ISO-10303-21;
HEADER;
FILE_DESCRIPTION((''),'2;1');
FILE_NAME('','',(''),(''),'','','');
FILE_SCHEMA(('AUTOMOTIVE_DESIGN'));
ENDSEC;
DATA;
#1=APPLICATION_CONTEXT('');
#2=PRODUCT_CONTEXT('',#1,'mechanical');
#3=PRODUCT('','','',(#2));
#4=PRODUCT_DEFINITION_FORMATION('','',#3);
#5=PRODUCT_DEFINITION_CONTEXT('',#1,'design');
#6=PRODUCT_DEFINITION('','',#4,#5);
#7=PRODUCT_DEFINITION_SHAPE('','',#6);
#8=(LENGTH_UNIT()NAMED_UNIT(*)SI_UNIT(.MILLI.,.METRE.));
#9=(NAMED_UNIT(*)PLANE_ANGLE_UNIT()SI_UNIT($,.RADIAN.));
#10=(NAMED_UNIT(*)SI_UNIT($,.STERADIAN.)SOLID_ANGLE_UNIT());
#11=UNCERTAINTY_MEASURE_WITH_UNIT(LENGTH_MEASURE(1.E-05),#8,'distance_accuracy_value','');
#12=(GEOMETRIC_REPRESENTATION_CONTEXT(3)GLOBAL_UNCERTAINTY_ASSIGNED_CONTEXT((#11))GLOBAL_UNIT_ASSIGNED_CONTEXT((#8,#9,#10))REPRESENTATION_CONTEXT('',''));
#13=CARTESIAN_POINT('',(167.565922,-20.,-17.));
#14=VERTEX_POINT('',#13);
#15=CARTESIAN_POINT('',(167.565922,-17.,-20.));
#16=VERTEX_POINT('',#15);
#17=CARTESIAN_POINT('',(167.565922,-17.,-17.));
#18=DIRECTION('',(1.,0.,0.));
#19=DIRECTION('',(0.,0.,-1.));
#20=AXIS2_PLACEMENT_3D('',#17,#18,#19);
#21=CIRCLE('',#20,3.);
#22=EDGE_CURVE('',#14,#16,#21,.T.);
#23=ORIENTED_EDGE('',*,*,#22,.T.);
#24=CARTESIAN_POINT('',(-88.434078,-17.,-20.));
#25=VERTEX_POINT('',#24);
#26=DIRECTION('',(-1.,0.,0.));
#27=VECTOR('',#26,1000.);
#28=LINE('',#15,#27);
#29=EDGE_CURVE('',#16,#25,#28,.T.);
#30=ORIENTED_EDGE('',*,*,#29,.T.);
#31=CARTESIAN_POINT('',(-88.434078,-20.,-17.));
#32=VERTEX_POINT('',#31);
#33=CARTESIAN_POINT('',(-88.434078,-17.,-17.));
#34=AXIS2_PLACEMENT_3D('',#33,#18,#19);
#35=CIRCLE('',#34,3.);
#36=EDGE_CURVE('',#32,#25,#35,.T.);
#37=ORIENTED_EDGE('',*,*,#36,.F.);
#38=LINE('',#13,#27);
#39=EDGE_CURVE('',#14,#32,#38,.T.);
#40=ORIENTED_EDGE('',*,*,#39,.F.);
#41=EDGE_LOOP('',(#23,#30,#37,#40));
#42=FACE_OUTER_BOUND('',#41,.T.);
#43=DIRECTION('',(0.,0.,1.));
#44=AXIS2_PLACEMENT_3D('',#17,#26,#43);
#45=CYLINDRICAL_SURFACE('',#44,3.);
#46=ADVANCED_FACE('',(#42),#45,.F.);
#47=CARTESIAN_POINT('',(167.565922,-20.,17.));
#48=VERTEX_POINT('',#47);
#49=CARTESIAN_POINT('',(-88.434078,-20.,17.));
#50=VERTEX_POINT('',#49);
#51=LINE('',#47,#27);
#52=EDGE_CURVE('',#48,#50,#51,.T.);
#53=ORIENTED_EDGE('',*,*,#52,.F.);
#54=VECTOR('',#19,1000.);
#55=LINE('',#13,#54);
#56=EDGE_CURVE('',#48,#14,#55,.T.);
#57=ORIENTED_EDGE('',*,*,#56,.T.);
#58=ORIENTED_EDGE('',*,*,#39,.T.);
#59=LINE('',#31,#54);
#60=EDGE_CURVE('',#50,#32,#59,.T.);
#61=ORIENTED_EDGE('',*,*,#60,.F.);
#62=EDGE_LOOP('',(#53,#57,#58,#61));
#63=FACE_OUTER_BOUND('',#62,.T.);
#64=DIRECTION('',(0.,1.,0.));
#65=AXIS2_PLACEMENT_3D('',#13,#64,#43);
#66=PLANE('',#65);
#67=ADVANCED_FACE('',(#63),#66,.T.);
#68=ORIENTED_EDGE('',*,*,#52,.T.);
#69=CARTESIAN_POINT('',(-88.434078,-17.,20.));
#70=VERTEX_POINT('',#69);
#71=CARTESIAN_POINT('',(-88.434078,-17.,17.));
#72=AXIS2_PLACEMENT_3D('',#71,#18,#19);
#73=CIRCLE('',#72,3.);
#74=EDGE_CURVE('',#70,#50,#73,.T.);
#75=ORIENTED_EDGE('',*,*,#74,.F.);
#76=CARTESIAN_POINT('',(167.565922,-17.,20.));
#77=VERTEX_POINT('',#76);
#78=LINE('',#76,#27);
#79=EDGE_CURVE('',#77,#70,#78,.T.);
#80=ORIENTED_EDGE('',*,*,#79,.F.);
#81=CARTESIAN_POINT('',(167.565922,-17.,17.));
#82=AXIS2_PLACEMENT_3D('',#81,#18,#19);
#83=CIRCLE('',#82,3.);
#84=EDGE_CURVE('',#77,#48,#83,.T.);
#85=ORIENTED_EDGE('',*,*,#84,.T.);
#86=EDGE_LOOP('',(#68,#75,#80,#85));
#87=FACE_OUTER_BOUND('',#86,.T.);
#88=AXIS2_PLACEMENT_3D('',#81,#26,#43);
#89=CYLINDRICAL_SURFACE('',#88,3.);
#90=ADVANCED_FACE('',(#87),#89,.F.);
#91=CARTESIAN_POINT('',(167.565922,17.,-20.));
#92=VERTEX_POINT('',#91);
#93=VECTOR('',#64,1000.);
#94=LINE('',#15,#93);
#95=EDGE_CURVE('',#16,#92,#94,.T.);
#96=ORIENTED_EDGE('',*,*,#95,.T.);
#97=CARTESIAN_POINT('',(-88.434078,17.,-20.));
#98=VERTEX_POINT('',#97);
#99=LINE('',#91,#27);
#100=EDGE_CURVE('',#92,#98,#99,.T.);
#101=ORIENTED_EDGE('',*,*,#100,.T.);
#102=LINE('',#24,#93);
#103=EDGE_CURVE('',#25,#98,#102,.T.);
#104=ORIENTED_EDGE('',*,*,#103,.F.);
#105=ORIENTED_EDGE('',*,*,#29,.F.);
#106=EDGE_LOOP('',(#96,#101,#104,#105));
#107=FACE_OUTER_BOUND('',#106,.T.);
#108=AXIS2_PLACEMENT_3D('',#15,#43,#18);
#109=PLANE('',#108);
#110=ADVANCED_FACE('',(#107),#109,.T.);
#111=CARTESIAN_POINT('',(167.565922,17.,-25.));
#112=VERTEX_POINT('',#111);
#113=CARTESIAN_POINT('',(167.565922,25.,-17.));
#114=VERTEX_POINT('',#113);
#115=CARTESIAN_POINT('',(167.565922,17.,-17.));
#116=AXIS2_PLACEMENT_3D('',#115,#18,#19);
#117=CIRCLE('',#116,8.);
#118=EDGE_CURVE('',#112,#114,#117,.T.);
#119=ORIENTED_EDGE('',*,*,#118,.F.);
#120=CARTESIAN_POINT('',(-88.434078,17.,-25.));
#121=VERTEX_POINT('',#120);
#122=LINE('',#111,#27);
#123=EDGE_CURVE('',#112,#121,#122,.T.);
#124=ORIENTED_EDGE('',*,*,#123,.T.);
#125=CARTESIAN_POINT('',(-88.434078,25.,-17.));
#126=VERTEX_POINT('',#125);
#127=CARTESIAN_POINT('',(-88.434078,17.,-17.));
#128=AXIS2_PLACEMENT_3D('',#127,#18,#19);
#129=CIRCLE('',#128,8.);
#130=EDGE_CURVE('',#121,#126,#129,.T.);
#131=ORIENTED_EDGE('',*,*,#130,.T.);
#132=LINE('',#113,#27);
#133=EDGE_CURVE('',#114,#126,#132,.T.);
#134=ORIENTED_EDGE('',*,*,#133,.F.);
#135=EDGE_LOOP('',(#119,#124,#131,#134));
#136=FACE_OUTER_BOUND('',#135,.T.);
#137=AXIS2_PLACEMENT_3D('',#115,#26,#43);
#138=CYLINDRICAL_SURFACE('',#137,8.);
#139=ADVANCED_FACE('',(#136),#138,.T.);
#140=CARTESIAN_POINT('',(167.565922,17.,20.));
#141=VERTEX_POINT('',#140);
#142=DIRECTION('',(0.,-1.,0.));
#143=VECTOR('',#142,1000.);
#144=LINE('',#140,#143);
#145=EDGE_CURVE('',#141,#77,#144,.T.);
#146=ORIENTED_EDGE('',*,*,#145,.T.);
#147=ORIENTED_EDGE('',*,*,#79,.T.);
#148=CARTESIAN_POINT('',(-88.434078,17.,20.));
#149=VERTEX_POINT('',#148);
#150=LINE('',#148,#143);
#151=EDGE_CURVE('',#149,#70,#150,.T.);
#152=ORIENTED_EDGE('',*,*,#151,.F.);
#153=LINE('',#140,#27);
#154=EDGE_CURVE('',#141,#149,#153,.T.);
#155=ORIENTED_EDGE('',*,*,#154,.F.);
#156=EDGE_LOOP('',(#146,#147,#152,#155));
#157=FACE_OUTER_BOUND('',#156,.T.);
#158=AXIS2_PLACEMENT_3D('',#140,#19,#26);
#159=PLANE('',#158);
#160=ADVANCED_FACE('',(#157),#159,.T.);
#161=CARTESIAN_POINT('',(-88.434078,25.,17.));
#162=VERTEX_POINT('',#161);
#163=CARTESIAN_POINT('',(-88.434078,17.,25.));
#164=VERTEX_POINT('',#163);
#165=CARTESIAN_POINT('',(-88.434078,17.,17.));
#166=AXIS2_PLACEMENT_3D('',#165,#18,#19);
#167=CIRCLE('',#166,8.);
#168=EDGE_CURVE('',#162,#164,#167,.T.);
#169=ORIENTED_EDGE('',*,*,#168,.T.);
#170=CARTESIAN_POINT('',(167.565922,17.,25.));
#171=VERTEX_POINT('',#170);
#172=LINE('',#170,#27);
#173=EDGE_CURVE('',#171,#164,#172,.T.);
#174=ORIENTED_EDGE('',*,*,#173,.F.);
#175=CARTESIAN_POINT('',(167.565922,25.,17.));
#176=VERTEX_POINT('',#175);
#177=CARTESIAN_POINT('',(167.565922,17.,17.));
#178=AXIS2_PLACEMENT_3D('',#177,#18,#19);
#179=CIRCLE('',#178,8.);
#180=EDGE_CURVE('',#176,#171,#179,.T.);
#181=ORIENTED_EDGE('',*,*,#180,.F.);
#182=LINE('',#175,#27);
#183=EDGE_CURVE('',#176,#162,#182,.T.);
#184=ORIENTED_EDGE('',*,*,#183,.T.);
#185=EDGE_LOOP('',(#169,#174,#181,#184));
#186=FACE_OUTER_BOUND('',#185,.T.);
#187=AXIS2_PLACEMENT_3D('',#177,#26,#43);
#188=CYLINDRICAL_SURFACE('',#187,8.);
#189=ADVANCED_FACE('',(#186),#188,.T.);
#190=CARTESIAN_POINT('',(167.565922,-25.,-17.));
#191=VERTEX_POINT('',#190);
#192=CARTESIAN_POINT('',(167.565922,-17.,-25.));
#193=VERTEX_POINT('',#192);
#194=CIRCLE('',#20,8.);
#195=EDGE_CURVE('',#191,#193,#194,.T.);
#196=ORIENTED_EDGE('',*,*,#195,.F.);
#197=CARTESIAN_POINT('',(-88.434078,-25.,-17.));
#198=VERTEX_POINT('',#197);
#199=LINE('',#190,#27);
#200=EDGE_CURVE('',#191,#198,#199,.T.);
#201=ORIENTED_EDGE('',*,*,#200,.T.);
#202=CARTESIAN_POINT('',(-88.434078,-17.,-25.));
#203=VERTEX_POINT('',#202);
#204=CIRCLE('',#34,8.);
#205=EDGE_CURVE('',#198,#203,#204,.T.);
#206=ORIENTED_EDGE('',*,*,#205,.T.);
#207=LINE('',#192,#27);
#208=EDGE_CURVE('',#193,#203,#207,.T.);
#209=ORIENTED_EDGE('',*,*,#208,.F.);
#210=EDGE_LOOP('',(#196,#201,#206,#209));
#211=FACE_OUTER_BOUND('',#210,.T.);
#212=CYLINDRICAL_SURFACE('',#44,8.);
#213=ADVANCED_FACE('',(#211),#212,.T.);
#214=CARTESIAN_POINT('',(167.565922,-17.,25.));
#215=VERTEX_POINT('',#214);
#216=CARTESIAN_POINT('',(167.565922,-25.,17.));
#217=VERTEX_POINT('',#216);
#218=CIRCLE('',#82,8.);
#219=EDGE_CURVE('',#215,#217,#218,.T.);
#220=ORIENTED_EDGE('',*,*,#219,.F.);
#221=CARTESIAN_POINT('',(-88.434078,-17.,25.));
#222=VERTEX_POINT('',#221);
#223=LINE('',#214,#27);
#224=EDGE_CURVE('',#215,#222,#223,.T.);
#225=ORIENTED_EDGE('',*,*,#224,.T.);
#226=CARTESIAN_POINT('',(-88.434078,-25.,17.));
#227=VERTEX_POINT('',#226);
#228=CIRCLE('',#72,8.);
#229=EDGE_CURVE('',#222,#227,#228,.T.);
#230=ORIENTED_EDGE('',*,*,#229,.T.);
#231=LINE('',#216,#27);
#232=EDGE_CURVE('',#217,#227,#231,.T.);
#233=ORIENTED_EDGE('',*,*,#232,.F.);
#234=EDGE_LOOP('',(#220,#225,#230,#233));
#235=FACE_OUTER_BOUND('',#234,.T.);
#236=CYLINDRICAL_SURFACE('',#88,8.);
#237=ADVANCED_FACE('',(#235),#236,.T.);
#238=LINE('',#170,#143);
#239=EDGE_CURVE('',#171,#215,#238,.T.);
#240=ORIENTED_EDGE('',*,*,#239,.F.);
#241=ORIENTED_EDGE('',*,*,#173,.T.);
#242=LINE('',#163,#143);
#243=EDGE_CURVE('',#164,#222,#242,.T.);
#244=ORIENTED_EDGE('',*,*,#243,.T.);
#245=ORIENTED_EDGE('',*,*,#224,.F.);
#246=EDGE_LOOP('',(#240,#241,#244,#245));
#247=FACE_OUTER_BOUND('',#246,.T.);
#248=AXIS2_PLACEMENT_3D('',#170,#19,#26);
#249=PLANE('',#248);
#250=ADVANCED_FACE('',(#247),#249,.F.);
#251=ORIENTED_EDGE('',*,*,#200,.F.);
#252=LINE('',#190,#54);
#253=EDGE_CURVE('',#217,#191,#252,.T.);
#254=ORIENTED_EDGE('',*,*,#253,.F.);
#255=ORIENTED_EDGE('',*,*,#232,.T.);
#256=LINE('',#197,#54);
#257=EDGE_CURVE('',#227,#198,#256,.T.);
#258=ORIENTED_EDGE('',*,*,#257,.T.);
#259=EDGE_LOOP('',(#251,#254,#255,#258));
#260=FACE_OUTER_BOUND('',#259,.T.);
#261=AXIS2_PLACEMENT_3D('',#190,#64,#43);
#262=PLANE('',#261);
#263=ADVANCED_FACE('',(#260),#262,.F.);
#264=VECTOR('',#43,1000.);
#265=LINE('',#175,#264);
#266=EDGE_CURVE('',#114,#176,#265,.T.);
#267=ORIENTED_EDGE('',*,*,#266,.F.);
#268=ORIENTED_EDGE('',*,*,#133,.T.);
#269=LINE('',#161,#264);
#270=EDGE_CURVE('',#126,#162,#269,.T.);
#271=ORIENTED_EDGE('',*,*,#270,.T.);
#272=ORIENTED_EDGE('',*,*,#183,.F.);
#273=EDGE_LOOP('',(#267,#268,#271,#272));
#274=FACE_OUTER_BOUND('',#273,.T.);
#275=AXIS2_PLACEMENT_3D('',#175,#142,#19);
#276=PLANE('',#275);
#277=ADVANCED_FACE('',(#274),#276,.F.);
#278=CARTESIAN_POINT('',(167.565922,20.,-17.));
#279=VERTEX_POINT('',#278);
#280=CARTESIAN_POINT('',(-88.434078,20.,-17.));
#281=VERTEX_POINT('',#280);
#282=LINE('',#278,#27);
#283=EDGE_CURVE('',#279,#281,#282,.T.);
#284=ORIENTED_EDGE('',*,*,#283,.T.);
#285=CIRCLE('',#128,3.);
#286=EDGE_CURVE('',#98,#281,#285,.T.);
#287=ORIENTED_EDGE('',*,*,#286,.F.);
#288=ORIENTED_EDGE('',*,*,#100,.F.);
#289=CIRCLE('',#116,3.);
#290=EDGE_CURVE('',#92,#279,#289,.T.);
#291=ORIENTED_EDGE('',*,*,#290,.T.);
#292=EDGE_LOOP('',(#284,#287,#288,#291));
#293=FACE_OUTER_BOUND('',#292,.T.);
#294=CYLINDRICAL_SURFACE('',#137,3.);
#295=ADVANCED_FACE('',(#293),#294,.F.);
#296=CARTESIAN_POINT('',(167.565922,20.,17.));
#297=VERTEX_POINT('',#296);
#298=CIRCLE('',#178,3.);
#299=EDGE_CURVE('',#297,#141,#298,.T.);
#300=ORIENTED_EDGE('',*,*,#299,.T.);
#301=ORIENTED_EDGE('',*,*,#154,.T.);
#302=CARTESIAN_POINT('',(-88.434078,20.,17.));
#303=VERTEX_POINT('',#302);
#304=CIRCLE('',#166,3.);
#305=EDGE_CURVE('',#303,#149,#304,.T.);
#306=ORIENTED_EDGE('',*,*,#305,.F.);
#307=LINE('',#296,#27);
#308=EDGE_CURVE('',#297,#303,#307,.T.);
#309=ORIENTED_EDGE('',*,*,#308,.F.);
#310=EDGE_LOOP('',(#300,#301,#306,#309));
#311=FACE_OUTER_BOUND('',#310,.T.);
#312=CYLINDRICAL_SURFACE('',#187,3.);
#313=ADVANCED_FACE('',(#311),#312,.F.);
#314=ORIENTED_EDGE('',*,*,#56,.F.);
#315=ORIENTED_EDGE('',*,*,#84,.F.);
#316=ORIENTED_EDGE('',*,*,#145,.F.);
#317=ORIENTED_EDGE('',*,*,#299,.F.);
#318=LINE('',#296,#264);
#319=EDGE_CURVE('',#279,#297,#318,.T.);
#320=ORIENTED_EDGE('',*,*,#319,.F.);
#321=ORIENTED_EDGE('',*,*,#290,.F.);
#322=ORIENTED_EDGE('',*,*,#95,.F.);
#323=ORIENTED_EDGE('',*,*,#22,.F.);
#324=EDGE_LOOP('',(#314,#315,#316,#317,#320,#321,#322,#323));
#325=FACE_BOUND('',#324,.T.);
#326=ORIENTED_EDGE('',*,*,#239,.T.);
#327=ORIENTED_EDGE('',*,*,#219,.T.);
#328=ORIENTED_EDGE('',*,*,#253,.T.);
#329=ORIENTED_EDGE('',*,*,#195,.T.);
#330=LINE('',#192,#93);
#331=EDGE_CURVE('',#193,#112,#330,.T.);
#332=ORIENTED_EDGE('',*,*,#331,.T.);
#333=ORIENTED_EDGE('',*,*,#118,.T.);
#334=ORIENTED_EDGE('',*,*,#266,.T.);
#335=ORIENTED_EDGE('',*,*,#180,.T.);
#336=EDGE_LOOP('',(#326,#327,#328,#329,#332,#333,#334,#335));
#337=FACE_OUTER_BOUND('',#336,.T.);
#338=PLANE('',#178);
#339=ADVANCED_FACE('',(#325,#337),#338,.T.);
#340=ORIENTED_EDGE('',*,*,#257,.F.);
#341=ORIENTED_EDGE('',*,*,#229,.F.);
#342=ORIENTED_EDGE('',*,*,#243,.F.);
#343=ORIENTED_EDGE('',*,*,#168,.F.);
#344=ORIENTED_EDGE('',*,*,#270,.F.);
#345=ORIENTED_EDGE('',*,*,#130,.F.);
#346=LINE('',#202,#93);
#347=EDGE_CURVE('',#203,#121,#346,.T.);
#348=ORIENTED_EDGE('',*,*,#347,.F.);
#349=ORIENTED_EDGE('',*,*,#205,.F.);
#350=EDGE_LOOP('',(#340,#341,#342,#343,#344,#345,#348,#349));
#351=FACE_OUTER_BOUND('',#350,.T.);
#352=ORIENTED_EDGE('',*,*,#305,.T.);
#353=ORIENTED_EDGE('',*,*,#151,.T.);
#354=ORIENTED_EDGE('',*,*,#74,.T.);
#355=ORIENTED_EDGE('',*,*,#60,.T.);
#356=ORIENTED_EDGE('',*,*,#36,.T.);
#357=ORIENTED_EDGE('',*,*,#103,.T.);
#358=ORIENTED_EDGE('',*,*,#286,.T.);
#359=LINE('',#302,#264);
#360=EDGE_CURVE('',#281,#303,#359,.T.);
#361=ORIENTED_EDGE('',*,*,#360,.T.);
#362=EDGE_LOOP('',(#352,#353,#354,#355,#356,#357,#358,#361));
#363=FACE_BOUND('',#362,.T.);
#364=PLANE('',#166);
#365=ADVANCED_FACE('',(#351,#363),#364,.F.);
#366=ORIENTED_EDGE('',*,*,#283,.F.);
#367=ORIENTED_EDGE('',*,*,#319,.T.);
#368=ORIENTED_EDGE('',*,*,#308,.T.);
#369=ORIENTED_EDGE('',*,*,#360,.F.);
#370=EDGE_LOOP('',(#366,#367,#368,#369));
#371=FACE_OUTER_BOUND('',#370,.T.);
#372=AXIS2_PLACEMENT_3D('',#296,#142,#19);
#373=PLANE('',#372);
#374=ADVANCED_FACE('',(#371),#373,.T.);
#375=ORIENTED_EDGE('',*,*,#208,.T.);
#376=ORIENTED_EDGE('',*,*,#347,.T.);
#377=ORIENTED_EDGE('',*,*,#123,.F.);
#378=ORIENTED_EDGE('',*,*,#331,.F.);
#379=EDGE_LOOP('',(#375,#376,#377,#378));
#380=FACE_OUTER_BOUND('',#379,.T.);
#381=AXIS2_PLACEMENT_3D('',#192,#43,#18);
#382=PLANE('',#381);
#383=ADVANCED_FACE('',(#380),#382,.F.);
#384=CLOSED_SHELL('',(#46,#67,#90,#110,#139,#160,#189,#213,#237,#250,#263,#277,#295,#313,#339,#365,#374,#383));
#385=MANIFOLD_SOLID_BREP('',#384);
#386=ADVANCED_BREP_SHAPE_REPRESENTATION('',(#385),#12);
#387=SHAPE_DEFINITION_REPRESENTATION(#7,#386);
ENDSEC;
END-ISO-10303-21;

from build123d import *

# Parameters (mm, degrees)
COLD_FORMED_SQUARE_HOLLOW_SECTION_GB_T_6_DEPTH = 256


with BuildPart() as part:
    # Sketch1 → Cold-formed square hollow section GB/T 6728-2002 50 X 50 X 4(1) (new body)
    with BuildSketch(Plane.YZ.offset(-88.434077868)):
        with BuildLine():
            Line((-17, -25), (17, -25))
            ThreePointArc((17, -25), (22.656854249, -22.656854249), (25, -17))
            Line((25, -17), (25, 17))
            ThreePointArc((25, 17), (22.656854249, 22.656854249), (17, 25))
            Line((17, 25), (-17, 25))
            ThreePointArc((-17, 25), (-22.656854249, 22.656854249), (-25, 17))
            Line((-25, 17), (-25, -17))
            ThreePointArc((-25, -17), (-22.656854249, -22.656854249), (-17, -25))
        make_face()
        with BuildLine():
            Line((-17, -20), (17, -20))
            ThreePointArc((17, -20), (19.121320344, -19.121320344), (20, -17))
            Line((20, -17), (20, 17))
            ThreePointArc((20, 17), (19.121320344, 19.121320344), (17, 20))
            Line((17, 20), (-17, 20))
            ThreePointArc((-17, 20), (-19.121320344, 19.121320344), (-20, 17))
            Line((-20, 17), (-20, -17))
            ThreePointArc((-20, -17), (-19.121320344, -19.121320344), (-17, -20))
        make_face(mode=Mode.SUBTRACT)
    extrude(amount=COLD_FORMED_SQUARE_HOLLOW_SECTION_GB_T_6_DEPTH)


solid = part.part
